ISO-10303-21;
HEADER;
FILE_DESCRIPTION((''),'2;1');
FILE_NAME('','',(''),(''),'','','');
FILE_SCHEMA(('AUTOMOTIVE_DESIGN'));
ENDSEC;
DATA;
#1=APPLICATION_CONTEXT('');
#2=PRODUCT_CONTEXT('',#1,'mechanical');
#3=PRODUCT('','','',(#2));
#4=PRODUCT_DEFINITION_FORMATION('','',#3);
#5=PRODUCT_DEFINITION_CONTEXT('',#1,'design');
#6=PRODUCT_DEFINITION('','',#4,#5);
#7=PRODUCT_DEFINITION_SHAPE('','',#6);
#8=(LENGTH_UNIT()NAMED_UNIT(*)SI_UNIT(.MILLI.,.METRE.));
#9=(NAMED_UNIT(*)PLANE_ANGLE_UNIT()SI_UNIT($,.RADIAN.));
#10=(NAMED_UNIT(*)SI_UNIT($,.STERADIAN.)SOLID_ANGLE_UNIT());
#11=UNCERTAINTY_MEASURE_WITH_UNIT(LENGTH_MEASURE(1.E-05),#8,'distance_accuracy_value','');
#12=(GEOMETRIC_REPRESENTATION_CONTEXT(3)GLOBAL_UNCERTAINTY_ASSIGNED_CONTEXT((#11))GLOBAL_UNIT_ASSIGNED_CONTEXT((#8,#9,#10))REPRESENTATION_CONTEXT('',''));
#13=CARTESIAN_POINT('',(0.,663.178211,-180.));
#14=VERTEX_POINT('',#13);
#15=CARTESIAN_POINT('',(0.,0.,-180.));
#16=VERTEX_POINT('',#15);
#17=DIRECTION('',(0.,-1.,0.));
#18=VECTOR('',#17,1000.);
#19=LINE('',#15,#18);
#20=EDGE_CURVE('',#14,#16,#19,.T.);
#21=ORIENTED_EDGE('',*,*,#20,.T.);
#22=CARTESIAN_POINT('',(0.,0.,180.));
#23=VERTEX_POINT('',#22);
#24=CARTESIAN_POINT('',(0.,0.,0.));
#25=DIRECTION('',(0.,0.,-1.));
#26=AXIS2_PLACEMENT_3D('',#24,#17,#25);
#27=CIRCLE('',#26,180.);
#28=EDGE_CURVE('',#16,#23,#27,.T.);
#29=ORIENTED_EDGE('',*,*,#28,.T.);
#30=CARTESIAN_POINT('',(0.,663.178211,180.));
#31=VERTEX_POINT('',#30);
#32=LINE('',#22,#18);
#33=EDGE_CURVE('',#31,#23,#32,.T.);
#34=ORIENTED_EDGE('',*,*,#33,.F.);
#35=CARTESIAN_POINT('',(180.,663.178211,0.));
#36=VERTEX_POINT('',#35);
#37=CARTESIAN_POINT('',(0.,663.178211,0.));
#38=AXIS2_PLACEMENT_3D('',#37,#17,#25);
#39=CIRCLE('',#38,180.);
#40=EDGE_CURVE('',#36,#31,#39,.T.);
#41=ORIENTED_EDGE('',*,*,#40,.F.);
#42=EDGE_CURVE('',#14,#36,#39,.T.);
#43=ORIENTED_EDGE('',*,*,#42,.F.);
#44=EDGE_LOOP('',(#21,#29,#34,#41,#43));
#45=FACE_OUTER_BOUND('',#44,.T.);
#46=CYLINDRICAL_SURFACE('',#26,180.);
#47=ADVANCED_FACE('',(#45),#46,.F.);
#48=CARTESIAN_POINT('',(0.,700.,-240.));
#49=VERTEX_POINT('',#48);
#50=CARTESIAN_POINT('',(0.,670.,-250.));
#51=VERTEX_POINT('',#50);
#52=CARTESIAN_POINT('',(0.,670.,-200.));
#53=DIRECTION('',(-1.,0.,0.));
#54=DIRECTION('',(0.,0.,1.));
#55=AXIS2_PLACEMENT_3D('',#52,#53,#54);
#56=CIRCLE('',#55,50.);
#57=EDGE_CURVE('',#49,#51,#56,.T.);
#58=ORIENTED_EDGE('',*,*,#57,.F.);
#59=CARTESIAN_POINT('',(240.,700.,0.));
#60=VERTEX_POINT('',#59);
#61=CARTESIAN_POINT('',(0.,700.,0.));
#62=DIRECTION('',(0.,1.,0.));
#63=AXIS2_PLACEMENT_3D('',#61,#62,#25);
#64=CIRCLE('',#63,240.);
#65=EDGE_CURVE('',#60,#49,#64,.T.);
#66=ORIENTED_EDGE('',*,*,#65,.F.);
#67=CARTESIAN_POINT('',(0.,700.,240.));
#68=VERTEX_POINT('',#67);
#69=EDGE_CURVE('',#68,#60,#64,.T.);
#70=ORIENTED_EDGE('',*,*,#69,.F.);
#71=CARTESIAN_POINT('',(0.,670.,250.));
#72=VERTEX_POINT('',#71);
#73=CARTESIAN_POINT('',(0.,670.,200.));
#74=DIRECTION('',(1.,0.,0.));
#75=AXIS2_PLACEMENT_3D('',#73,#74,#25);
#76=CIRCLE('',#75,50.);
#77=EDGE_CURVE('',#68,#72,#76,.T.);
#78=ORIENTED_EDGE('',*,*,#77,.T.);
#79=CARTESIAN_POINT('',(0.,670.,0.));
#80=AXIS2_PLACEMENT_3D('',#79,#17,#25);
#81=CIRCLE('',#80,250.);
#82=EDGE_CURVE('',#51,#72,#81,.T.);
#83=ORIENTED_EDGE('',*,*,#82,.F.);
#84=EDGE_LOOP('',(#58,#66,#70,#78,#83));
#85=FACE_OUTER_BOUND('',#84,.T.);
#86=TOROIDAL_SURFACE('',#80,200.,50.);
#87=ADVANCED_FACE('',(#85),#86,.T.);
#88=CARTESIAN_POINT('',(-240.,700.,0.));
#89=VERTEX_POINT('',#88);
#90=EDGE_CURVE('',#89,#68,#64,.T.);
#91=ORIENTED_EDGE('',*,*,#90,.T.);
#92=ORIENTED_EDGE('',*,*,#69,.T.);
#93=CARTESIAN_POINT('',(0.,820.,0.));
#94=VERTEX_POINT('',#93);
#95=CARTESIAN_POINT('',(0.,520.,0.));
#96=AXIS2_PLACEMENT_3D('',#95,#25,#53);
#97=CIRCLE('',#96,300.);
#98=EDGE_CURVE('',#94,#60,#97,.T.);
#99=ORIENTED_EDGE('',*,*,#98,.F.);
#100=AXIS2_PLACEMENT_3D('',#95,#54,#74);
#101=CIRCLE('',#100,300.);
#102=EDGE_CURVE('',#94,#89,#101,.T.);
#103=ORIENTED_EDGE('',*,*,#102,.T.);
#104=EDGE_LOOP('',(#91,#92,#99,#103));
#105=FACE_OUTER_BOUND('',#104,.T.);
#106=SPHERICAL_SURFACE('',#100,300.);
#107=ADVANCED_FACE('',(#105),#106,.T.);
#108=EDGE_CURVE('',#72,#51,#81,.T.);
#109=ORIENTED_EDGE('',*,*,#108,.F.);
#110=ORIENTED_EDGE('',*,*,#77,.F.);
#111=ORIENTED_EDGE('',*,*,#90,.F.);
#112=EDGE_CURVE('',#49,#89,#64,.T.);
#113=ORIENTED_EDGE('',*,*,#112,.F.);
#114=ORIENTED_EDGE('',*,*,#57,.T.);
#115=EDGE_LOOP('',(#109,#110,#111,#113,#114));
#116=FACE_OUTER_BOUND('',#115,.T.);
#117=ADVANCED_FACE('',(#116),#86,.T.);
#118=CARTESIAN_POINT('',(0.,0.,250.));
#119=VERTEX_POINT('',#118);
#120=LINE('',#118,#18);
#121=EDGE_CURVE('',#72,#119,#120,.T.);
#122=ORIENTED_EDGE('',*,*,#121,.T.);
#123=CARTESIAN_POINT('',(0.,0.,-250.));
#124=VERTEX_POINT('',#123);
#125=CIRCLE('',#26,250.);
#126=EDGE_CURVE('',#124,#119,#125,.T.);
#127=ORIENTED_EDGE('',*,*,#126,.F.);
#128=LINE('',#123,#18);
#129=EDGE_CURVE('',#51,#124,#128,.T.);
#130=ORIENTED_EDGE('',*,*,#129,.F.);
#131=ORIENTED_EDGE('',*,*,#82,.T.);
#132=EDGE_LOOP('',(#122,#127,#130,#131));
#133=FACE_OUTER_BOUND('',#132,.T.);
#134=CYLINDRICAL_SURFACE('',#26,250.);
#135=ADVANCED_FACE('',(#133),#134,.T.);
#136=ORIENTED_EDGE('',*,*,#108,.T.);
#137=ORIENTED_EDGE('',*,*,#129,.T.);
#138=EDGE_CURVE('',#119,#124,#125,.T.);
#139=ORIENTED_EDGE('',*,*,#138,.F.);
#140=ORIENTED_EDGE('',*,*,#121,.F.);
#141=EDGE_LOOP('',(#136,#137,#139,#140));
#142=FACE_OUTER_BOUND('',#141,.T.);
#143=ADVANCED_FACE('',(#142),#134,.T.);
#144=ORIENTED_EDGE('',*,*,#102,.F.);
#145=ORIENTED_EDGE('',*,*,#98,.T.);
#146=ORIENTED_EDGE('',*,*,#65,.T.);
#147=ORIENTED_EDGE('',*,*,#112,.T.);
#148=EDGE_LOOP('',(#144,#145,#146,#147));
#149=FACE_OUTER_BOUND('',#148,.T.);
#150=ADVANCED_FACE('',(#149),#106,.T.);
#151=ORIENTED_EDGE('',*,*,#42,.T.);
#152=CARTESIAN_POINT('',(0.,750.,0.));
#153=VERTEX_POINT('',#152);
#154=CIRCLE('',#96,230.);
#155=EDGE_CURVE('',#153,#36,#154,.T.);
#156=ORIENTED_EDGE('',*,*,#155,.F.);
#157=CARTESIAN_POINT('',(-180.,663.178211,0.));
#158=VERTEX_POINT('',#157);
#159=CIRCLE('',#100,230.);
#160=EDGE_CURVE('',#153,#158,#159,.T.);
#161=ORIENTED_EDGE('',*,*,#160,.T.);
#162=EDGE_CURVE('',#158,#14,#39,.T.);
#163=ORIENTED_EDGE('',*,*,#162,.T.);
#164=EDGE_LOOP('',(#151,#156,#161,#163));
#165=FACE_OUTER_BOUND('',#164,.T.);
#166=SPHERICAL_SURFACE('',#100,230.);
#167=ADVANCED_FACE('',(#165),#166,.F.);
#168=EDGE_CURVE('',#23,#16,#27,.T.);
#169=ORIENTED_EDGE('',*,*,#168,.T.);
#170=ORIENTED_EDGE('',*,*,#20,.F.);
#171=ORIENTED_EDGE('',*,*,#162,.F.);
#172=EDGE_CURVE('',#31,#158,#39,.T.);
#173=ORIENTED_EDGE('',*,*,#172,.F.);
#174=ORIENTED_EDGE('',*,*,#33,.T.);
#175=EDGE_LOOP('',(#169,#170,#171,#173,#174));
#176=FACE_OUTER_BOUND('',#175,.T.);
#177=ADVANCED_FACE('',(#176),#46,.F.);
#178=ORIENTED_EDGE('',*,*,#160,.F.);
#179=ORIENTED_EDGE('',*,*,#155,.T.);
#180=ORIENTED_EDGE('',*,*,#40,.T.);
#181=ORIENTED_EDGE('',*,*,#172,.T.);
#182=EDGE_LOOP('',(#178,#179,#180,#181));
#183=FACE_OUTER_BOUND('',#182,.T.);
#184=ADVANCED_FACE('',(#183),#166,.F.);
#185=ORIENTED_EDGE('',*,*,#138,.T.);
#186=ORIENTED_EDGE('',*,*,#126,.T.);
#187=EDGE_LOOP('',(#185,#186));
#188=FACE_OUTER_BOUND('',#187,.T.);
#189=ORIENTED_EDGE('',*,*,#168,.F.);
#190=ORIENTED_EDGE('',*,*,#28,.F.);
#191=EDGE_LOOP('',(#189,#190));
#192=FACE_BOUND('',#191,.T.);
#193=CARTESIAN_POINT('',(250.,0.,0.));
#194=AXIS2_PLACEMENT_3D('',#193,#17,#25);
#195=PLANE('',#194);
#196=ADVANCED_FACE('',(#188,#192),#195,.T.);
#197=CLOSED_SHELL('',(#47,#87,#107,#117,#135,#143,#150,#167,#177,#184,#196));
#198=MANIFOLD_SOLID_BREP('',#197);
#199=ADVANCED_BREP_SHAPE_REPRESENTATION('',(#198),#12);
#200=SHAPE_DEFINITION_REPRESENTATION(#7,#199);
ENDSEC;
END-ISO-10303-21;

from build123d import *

# Parameters (mm, degrees)
FILLET1_R = 50
SHELL1_T  = -70


with BuildPart() as part:
    # Sketch1 → Revolve1 (revolve)
    with BuildSketch(Plane.XY, mode=Mode.PRIVATE) as revolve1_sk:
        with BuildLine():
            Line((0, 0), (0, 700))
            Line((0, 700), (0, 820))
            ThreePointArc((0, 820), (141.863716546, 784.338203685), (250, 685.831239518))
            Line((250, 685.831239518), (250, 0))
            Line((250, 0), (0, 0))
        make_face()
    revolve(revolve1_sk.sketch.rotate(Axis((0, 0, 0), (0, 1, 0)), 90), axis=Axis((0, 0, 0), (0, 1, 0)))

    # Fillet1
    fillet1_edges = [part.edges().sort_by_distance(p)[0] for p in [
        (0, 685.831239518, 250),
    ]]
    fillet(fillet1_edges, radius=FILLET1_R)

    # Shell1
    shell1_openings = [part.faces().sort_by_distance(p)[0] for p in [
        (0, 0, 0),
    ]]
    offset(amount=SHELL1_T, openings=shell1_openings, kind=Kind.INTERSECTION)


solid = part.part
